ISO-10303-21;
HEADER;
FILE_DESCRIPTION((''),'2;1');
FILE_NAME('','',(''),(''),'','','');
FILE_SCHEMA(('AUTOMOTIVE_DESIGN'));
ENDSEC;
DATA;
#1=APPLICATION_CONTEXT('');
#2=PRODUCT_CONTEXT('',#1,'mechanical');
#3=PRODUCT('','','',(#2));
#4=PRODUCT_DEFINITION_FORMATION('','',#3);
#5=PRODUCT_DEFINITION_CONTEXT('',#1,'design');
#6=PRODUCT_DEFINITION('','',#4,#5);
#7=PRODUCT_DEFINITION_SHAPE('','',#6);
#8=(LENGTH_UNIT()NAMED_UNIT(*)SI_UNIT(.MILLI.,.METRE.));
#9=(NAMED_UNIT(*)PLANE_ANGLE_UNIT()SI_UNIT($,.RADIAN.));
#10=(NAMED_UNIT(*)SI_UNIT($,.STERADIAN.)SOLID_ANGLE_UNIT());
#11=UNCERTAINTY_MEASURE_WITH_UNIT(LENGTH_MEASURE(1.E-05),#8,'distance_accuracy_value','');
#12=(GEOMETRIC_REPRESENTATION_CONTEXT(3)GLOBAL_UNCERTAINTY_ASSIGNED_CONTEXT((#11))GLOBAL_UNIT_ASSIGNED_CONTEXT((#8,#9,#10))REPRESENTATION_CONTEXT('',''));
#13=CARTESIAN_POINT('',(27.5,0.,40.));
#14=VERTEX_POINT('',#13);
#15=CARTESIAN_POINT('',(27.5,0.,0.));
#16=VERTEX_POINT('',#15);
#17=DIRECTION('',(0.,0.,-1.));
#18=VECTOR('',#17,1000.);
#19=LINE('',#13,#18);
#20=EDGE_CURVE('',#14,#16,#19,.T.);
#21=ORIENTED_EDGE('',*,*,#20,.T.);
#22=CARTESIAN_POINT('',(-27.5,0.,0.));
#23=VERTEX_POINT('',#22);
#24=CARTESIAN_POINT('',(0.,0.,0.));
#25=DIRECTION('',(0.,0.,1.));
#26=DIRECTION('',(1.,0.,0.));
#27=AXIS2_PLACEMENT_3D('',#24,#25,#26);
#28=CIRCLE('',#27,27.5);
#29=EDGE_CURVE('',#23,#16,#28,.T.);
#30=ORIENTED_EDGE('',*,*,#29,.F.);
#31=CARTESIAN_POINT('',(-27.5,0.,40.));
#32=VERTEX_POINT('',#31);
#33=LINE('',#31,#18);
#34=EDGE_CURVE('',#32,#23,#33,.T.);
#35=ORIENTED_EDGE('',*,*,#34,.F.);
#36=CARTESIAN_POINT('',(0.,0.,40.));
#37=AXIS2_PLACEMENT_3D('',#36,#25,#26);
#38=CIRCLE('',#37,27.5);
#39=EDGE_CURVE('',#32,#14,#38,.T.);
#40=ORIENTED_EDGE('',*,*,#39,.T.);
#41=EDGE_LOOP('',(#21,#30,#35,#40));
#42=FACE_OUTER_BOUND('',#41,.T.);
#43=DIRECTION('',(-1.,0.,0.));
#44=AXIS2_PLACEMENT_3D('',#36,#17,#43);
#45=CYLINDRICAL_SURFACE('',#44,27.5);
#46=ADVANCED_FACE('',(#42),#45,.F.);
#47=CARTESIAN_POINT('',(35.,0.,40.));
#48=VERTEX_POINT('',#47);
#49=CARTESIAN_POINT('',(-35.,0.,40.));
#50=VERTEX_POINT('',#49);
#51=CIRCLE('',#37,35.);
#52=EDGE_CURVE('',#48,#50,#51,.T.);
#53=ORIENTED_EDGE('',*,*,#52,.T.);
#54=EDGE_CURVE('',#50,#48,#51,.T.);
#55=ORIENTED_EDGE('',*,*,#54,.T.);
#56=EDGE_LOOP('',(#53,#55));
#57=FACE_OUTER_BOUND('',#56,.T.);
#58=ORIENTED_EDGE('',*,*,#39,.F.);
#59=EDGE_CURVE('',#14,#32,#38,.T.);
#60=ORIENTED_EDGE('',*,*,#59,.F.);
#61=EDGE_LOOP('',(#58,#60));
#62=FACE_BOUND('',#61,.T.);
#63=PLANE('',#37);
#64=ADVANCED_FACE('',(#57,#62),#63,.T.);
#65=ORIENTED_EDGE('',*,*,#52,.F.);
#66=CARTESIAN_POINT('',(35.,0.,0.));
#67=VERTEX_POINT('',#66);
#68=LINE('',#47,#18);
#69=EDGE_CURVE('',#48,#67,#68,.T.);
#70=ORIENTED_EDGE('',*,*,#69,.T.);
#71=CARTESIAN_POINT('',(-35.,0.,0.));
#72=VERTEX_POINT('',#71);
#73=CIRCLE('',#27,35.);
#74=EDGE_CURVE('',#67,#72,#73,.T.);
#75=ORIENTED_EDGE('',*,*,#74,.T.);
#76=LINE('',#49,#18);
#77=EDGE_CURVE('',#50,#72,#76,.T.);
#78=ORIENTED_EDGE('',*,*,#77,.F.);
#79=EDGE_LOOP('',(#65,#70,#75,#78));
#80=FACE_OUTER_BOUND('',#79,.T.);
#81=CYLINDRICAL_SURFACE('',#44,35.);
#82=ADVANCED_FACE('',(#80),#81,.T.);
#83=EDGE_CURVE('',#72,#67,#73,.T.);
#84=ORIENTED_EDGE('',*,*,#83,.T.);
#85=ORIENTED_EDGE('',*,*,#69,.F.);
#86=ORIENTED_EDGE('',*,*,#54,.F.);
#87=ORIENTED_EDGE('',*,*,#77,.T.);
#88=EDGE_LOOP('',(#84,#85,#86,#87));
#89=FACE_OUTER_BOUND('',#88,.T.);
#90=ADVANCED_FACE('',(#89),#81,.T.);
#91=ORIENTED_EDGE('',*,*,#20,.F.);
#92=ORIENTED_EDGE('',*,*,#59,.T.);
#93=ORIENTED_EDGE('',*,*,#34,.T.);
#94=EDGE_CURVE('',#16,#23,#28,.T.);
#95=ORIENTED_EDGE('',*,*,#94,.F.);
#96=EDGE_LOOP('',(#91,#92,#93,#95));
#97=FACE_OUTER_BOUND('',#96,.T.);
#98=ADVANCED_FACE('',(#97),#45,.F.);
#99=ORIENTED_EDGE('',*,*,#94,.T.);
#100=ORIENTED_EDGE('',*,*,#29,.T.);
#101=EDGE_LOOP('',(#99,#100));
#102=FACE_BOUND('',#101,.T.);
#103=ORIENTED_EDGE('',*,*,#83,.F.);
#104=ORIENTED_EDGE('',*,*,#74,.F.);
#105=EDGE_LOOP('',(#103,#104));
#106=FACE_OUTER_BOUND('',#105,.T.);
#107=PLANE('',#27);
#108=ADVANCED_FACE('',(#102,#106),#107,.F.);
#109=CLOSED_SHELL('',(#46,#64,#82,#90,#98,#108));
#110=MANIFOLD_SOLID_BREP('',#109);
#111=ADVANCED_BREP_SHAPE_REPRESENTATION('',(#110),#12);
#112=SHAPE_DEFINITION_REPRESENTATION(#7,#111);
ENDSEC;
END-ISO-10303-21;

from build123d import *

# Parameters (mm, degrees)
SKETCH_1_R      = 35
SKETCH_1_R_2    = 27.5
EXTRUDE_1_DEPTH = 40


with BuildPart() as part:
    # 草图1 → 凸台-拉伸1 (new body)
    with BuildSketch(Plane.XY):
        Circle(SKETCH_1_R)
        Circle(SKETCH_1_R_2, mode=Mode.SUBTRACT)
    extrude(amount=EXTRUDE_1_DEPTH)


solid = part.part
